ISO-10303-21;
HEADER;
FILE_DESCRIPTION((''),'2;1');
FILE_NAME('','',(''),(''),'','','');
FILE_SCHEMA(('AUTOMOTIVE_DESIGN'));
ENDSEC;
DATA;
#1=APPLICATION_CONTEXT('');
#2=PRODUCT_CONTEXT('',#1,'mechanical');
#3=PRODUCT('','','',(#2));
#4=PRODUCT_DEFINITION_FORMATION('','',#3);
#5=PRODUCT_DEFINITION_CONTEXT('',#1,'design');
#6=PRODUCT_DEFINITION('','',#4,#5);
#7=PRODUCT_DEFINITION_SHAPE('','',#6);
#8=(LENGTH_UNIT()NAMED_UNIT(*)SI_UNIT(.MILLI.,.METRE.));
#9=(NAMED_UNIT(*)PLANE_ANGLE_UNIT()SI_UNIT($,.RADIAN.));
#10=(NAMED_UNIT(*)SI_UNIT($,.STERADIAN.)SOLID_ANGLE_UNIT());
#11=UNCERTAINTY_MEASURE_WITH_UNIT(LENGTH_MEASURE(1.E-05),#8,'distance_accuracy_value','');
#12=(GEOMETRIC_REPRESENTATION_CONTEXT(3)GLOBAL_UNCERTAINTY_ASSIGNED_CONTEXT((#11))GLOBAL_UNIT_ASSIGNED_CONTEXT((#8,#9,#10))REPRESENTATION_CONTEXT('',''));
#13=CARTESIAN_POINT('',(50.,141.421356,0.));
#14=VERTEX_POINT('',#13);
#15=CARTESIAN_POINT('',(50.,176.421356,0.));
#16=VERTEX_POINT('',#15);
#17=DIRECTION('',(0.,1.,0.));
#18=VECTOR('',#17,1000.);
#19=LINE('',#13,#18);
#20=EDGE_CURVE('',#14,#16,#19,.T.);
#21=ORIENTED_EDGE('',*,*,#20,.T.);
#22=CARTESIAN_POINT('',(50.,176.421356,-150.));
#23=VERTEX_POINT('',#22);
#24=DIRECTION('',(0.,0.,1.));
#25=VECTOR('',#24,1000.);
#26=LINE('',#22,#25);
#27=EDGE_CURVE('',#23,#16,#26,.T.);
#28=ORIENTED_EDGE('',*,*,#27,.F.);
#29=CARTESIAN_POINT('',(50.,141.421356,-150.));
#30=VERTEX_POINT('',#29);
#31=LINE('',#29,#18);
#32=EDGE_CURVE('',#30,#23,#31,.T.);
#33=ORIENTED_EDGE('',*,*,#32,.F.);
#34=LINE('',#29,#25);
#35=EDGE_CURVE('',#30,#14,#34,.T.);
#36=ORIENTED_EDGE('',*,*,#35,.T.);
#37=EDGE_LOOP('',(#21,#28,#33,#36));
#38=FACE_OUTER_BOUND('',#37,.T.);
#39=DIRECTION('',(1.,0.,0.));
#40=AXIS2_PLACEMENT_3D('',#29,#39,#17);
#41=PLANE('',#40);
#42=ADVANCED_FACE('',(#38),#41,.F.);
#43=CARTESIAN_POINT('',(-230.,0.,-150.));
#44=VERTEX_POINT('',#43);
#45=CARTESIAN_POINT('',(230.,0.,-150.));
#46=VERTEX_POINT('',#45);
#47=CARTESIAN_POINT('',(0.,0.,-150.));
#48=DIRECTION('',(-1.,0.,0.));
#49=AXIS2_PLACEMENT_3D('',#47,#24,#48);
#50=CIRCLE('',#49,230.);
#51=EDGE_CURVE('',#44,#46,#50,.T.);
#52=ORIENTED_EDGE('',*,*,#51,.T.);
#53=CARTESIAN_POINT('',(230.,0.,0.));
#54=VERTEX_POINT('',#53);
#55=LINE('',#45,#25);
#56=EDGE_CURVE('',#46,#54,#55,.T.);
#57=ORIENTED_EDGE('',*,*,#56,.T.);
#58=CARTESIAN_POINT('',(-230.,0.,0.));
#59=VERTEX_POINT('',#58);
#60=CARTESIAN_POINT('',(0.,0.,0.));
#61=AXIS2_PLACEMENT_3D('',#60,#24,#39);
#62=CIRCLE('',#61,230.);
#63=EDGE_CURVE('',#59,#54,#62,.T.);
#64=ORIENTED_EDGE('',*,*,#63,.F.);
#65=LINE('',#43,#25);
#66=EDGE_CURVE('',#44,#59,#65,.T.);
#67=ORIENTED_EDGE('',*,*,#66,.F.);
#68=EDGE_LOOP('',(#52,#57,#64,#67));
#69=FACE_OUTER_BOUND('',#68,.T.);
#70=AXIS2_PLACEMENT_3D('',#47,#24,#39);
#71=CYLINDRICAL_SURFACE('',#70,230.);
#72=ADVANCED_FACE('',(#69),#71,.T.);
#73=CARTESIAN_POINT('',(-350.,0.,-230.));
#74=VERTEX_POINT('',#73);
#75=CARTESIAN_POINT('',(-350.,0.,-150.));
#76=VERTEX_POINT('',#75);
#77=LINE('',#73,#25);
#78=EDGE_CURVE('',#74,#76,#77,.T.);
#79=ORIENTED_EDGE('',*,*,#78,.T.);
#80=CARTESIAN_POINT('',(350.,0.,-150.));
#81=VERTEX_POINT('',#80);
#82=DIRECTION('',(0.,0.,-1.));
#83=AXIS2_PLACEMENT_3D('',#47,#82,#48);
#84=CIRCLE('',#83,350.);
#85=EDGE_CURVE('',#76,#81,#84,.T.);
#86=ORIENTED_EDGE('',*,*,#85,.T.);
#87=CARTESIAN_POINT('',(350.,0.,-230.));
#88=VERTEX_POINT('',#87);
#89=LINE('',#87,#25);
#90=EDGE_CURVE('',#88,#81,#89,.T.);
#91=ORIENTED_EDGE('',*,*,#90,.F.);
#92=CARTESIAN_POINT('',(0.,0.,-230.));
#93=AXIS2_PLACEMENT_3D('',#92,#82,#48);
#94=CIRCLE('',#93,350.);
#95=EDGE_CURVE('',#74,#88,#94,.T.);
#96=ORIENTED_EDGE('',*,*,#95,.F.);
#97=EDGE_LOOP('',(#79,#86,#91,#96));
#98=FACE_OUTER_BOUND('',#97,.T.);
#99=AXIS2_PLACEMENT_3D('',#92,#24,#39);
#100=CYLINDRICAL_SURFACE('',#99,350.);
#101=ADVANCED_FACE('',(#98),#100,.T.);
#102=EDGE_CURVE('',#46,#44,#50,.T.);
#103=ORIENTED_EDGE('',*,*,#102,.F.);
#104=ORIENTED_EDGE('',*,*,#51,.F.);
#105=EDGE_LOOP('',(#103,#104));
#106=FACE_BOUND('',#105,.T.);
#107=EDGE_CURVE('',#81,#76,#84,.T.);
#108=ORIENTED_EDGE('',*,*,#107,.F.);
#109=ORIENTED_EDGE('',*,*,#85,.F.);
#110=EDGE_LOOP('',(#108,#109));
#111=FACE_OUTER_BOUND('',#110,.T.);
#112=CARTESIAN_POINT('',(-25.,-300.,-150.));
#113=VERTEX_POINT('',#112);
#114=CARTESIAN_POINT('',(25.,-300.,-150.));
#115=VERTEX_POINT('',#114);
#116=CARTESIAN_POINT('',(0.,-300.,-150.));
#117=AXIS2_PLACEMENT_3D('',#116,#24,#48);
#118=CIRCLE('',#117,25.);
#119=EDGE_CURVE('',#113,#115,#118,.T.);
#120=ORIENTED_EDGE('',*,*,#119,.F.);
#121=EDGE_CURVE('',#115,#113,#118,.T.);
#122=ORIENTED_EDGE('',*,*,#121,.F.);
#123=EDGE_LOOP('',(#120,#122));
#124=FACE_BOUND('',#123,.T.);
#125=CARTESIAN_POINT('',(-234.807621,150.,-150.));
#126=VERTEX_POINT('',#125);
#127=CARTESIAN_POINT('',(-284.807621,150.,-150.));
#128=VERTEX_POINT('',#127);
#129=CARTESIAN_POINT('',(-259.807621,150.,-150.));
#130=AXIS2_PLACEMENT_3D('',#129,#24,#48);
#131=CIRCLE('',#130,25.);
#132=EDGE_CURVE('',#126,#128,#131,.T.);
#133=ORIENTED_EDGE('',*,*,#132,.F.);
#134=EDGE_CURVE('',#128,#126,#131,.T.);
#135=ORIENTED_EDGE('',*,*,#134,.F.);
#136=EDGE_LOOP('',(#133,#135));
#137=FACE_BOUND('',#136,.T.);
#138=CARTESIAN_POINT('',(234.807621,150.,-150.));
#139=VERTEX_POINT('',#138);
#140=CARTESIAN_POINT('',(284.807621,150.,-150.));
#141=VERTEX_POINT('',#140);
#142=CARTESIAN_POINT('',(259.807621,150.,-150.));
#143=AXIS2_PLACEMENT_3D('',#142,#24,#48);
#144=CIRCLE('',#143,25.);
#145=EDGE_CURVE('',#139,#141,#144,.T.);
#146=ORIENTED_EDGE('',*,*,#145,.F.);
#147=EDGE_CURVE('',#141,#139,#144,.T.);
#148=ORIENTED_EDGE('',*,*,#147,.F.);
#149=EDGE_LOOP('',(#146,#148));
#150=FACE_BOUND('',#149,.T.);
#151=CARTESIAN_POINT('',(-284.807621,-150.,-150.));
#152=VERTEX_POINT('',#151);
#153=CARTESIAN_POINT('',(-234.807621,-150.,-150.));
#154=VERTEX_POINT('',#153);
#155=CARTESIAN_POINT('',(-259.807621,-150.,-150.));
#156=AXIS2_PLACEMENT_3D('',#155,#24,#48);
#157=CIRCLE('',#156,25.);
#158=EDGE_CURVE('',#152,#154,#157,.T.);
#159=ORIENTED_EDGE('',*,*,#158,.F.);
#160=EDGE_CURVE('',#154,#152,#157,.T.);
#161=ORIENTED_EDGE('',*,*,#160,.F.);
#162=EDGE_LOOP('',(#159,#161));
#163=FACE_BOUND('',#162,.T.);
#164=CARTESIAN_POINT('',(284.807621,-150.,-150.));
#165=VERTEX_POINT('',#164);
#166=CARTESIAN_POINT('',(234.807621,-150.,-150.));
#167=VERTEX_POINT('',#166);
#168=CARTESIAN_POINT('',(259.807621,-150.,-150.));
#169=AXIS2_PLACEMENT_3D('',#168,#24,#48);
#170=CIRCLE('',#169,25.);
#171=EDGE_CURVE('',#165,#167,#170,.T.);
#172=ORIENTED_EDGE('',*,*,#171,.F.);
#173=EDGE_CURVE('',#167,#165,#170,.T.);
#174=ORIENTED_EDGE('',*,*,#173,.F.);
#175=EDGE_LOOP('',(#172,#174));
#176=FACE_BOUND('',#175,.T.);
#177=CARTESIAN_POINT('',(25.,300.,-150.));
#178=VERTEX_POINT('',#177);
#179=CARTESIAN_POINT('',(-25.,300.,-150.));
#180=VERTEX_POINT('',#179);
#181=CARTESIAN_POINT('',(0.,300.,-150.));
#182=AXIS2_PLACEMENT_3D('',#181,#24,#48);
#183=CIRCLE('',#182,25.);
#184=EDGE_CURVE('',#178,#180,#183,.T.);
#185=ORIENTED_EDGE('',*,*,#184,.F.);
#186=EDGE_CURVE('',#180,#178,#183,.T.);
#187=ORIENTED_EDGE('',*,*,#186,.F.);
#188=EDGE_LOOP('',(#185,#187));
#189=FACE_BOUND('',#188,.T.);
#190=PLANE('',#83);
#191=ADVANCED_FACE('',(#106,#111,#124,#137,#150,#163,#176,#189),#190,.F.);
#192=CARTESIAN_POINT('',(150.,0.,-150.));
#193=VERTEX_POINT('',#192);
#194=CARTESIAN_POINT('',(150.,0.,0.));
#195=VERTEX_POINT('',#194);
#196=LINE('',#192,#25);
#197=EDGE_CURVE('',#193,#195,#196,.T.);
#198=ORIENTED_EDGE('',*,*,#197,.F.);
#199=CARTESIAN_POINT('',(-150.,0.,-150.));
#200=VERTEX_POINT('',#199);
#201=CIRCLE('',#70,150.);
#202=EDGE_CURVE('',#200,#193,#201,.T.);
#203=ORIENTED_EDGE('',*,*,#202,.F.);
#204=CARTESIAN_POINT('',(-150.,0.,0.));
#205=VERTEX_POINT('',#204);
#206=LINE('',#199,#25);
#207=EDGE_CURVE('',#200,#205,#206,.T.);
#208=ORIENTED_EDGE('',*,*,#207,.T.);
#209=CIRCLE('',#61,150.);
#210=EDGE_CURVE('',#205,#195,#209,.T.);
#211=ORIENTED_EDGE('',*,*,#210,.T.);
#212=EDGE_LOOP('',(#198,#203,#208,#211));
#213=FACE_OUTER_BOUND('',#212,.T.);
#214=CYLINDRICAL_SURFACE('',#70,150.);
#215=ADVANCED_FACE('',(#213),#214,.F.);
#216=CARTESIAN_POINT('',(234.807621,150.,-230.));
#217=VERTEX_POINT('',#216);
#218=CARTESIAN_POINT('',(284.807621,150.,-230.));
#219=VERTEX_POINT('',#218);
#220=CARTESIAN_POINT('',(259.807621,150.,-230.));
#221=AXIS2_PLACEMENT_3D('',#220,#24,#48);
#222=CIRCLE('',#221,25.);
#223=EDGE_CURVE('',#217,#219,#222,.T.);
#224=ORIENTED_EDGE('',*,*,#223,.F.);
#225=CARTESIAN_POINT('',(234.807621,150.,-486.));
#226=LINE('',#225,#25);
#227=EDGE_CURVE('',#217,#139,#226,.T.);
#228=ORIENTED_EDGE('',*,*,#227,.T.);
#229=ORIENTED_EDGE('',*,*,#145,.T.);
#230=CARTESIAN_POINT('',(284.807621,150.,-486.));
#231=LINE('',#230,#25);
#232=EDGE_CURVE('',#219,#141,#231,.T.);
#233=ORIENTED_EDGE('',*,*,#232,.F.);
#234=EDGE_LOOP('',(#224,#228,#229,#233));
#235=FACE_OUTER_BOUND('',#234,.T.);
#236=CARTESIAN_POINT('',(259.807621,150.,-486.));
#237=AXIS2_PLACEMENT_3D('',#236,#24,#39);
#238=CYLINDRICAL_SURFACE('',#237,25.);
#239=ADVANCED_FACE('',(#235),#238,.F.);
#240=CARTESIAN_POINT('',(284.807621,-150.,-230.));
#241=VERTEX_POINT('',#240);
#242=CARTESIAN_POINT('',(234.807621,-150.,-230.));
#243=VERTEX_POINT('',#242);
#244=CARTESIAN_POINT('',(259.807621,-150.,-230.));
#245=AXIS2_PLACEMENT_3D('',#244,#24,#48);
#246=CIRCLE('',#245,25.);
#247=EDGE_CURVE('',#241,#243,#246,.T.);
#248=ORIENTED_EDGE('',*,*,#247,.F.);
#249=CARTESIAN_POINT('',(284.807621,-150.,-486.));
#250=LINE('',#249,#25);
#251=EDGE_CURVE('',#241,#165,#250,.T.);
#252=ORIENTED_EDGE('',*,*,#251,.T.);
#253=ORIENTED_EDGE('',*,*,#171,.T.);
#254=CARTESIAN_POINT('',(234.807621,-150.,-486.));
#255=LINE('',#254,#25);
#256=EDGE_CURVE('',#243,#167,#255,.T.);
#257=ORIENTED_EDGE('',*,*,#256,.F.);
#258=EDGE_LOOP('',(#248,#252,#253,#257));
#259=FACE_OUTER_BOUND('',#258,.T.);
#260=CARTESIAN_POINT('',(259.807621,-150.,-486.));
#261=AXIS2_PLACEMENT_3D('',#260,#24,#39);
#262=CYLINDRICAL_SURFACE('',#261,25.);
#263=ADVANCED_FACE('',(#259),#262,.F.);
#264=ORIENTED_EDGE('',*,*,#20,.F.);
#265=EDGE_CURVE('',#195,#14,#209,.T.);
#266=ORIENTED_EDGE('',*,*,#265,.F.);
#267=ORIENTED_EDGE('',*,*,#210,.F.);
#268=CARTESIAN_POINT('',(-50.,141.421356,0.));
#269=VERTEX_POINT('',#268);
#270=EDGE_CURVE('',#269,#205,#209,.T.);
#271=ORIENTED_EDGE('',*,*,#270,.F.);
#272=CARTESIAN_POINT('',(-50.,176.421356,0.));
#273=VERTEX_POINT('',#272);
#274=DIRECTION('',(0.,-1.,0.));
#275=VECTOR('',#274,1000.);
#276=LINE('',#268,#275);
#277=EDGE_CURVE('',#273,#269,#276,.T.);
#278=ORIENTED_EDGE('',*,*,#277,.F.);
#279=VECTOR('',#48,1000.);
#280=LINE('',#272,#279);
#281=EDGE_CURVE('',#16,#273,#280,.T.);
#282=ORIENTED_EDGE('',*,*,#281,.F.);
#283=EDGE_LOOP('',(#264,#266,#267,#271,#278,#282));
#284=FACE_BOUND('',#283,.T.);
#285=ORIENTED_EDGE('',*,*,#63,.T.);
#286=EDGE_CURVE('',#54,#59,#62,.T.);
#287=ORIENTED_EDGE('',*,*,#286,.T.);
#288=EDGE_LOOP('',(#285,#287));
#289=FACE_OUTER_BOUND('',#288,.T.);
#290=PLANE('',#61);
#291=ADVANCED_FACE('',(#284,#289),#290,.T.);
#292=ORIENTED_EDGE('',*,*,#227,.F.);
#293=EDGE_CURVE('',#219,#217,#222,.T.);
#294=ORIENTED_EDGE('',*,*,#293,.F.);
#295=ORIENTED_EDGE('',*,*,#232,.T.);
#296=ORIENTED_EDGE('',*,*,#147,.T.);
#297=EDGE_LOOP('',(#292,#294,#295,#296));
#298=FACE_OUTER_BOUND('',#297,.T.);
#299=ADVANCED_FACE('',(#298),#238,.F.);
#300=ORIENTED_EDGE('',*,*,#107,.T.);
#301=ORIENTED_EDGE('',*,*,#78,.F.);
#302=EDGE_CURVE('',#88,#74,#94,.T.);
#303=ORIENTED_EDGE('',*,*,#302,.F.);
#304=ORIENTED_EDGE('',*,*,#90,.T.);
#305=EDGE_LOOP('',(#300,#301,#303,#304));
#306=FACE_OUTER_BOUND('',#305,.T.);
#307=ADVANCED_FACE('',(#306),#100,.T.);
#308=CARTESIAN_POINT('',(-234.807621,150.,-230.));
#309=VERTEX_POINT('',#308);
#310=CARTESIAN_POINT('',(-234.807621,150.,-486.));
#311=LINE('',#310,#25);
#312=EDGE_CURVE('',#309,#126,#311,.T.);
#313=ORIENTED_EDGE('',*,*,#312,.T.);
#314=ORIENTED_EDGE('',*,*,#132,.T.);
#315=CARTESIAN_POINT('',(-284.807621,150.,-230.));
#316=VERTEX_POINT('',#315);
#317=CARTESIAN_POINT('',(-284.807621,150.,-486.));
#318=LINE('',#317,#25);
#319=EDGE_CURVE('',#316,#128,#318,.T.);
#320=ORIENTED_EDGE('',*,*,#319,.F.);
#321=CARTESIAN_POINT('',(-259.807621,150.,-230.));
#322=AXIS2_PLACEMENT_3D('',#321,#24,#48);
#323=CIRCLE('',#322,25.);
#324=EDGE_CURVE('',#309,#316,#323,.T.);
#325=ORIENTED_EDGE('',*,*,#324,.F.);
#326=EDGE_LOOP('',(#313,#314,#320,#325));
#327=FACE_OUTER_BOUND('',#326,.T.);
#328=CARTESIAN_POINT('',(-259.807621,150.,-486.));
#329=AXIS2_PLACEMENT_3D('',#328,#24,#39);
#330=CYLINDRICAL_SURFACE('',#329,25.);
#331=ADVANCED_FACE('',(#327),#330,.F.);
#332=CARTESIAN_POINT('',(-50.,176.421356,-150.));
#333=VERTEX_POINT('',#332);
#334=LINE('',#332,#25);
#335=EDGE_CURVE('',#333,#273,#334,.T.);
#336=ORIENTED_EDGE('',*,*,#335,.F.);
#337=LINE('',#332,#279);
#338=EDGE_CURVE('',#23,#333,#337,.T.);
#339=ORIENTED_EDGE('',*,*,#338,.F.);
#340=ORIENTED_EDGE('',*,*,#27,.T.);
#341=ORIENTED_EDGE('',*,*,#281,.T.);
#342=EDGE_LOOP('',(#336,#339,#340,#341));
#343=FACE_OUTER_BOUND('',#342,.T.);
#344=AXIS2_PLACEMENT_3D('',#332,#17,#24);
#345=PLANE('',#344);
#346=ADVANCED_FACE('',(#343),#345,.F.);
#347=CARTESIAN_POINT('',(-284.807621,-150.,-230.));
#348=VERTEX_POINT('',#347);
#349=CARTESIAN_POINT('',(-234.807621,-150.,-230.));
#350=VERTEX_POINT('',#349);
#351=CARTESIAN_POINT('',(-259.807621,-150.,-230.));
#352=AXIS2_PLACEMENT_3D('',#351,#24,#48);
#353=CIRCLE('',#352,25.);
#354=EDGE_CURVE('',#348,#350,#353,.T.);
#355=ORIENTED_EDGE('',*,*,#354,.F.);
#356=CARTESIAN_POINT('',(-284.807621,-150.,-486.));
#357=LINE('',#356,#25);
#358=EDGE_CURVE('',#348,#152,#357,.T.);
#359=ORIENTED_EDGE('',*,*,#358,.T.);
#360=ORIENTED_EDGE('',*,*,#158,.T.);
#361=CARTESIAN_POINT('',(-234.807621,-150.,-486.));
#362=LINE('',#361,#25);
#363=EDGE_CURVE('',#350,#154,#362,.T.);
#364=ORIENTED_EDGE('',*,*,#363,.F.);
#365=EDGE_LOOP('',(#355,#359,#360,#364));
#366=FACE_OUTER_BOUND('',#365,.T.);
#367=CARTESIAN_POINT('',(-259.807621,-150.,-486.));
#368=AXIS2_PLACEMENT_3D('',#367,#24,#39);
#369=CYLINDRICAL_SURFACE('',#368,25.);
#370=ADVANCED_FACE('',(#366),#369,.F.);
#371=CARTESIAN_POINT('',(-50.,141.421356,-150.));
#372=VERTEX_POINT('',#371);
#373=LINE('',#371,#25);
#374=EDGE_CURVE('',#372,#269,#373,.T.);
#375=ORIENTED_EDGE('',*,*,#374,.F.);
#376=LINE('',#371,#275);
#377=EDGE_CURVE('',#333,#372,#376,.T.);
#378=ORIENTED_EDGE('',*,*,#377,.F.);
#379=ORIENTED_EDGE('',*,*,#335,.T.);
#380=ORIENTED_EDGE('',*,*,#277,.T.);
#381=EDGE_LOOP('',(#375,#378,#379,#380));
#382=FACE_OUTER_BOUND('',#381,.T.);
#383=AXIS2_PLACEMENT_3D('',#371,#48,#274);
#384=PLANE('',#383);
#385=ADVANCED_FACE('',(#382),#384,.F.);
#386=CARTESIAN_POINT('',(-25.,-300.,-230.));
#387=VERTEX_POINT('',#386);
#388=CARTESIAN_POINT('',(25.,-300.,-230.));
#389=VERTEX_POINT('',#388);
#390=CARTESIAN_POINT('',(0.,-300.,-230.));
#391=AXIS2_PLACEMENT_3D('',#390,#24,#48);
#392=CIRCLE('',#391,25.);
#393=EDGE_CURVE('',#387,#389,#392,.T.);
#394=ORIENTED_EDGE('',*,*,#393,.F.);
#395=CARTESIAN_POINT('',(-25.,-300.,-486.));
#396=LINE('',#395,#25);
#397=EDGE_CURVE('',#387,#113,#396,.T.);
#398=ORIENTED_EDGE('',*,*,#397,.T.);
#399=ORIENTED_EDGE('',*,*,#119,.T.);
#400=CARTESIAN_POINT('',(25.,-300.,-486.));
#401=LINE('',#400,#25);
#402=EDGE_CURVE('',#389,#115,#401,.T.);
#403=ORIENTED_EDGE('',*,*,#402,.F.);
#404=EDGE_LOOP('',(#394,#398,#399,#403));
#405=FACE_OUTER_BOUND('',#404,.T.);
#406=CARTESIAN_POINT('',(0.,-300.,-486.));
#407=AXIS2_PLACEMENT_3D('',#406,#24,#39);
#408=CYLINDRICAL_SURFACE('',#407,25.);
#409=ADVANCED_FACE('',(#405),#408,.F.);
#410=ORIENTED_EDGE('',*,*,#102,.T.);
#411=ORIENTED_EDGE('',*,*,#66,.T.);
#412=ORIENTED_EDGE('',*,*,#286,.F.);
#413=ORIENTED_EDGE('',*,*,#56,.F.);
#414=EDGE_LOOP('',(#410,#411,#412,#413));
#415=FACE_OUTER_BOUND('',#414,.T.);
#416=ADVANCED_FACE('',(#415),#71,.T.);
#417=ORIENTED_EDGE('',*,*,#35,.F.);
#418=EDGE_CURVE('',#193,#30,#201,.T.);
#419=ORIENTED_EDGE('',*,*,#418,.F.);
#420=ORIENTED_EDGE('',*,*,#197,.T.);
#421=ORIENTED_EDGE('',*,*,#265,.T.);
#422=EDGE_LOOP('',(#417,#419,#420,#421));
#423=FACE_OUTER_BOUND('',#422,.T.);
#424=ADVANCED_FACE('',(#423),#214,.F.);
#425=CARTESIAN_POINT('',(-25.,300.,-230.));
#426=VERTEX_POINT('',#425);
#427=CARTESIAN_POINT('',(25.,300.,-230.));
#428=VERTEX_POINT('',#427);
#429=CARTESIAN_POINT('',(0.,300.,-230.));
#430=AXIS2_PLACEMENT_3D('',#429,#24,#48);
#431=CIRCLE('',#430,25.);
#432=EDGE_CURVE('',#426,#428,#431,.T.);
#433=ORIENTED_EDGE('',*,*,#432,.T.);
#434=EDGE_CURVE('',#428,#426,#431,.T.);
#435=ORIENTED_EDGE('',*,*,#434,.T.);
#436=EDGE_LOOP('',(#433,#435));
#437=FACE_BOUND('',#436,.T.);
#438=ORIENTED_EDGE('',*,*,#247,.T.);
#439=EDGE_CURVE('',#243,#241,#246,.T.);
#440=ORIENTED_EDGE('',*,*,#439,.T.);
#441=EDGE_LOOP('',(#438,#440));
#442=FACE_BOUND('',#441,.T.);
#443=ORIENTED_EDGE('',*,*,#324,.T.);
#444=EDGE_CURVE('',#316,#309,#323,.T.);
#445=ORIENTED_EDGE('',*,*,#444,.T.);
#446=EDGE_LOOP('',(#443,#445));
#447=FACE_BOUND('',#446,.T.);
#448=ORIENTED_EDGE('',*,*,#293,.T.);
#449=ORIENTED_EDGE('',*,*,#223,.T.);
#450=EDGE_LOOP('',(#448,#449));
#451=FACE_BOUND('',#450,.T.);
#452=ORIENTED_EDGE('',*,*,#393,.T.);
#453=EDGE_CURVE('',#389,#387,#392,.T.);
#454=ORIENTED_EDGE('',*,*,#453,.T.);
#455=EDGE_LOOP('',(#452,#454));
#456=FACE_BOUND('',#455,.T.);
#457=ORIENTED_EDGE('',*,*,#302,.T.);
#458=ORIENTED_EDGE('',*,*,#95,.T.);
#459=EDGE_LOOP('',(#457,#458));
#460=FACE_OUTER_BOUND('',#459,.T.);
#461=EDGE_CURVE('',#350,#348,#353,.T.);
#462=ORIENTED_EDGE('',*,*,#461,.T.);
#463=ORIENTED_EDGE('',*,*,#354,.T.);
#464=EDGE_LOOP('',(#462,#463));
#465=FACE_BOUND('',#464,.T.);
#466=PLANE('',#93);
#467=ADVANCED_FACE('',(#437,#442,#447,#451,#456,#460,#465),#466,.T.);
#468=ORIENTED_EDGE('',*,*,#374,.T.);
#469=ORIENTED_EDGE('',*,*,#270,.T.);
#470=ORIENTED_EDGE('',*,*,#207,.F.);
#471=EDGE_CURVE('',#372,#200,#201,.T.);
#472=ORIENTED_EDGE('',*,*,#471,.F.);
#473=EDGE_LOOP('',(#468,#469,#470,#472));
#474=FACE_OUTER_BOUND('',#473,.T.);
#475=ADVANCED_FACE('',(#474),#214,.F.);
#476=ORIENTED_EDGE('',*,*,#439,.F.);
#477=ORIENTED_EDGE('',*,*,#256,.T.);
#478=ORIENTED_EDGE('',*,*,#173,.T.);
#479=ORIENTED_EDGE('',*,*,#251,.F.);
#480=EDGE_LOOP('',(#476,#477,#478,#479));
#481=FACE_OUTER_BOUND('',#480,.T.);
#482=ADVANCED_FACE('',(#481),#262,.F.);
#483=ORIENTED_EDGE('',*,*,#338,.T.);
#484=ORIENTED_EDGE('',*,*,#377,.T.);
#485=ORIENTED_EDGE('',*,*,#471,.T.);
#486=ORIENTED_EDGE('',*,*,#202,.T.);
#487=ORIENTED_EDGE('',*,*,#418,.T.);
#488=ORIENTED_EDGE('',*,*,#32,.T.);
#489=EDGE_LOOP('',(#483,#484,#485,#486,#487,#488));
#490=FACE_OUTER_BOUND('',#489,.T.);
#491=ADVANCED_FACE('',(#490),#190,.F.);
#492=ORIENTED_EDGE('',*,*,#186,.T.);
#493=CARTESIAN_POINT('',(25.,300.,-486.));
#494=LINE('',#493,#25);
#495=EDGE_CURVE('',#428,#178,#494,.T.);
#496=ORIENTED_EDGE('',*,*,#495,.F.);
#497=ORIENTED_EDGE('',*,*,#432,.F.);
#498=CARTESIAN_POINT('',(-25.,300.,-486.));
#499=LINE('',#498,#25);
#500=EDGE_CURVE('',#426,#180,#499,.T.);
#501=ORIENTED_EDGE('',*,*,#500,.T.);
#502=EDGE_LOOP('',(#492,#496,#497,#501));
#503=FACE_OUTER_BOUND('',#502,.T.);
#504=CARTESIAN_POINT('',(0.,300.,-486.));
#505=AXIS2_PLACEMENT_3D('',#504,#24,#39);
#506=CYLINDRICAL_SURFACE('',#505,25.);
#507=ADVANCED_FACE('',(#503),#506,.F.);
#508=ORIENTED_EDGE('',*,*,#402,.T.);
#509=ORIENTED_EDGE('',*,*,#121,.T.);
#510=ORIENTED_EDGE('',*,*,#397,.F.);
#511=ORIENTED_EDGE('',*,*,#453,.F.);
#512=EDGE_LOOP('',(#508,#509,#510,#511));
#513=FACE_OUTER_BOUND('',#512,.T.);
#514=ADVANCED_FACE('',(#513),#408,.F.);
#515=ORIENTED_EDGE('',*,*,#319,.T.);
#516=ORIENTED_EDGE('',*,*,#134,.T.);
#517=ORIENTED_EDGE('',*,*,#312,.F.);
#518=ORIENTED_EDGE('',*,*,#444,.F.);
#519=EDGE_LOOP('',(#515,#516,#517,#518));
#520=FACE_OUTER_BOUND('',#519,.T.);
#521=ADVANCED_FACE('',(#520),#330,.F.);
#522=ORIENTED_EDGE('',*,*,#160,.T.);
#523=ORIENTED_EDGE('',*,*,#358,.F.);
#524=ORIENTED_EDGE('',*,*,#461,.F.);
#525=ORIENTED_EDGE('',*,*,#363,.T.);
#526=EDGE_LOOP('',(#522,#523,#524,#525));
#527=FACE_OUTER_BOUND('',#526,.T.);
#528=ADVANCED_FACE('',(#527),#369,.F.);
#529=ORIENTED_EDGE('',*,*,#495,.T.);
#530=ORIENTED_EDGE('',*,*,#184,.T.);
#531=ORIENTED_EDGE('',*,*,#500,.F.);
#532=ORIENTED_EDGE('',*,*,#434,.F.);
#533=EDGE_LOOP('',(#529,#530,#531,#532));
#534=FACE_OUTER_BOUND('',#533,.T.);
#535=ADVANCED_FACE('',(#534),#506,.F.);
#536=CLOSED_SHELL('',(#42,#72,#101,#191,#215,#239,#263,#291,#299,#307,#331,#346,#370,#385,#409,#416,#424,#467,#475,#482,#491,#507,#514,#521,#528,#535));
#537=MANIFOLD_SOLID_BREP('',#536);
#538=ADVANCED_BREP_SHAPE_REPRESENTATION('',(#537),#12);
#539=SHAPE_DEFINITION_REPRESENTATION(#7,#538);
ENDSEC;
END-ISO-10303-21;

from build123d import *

# Parameters (mm, degrees)
SKETCH1_R               = 230
BOSS_EXTRUDE1_DEPTH     = 150
SKETCH2_R               = 350
BOSS_EXTRUDE2_DEPTH     = 80
CUT_EXTRUDE1_DEPTH      = 256
CUT_EXTRUDE1_DEPTH_BACK = 269
SKETCH3_R               = 25


with BuildPart() as part:
    # Sketch1 → Boss-Extrude1 (new body)
    with BuildSketch(Plane.XY):
        Circle(SKETCH1_R)
        with BuildLine():
            Line((-50, 141.421356237), (-50, 176.421356237))
            Line((-50, 176.421356237), (50, 176.421356237))
            Line((50, 176.421356237), (50, 141.421356237))
            ThreePointArc((50, 141.421356237), (0, -150), (-50, 141.421356237))
        make_face(mode=Mode.SUBTRACT)
    extrude(amount=-BOSS_EXTRUDE1_DEPTH)

    # Sketch2 → Boss-Extrude2 (add)
    with BuildSketch(Plane(origin=(0, 0, -150), x_dir=(-1, 0, 0), z_dir=(0, 0, -1))):
        Circle(SKETCH2_R)
    extrude(amount=BOSS_EXTRUDE2_DEPTH)

    # Sketch3 → Cut-Extrude1 (cut, two sides: drawn at the far end of the back side and taken through both)
    with BuildSketch(Plane(origin=(0, 0, -230), x_dir=(-1, 0, 0), z_dir=(0, 0, -1)).offset(-CUT_EXTRUDE1_DEPTH_BACK)):
        with Locations((0, 300)):
            Circle(SKETCH3_R)
        with Locations((259.807621135, 150)):
            Circle(SKETCH3_R)
        with Locations((259.807621135, -150)):
            Circle(SKETCH3_R)
        with Locations((0, -300)):
            Circle(SKETCH3_R)
        with Locations((-259.807621135, -150)):
            Circle(SKETCH3_R)
        with Locations((-259.807621135, 150)):
            Circle(SKETCH3_R)
    extrude(amount=CUT_EXTRUDE1_DEPTH + CUT_EXTRUDE1_DEPTH_BACK, mode=Mode.SUBTRACT)


solid = part.part
